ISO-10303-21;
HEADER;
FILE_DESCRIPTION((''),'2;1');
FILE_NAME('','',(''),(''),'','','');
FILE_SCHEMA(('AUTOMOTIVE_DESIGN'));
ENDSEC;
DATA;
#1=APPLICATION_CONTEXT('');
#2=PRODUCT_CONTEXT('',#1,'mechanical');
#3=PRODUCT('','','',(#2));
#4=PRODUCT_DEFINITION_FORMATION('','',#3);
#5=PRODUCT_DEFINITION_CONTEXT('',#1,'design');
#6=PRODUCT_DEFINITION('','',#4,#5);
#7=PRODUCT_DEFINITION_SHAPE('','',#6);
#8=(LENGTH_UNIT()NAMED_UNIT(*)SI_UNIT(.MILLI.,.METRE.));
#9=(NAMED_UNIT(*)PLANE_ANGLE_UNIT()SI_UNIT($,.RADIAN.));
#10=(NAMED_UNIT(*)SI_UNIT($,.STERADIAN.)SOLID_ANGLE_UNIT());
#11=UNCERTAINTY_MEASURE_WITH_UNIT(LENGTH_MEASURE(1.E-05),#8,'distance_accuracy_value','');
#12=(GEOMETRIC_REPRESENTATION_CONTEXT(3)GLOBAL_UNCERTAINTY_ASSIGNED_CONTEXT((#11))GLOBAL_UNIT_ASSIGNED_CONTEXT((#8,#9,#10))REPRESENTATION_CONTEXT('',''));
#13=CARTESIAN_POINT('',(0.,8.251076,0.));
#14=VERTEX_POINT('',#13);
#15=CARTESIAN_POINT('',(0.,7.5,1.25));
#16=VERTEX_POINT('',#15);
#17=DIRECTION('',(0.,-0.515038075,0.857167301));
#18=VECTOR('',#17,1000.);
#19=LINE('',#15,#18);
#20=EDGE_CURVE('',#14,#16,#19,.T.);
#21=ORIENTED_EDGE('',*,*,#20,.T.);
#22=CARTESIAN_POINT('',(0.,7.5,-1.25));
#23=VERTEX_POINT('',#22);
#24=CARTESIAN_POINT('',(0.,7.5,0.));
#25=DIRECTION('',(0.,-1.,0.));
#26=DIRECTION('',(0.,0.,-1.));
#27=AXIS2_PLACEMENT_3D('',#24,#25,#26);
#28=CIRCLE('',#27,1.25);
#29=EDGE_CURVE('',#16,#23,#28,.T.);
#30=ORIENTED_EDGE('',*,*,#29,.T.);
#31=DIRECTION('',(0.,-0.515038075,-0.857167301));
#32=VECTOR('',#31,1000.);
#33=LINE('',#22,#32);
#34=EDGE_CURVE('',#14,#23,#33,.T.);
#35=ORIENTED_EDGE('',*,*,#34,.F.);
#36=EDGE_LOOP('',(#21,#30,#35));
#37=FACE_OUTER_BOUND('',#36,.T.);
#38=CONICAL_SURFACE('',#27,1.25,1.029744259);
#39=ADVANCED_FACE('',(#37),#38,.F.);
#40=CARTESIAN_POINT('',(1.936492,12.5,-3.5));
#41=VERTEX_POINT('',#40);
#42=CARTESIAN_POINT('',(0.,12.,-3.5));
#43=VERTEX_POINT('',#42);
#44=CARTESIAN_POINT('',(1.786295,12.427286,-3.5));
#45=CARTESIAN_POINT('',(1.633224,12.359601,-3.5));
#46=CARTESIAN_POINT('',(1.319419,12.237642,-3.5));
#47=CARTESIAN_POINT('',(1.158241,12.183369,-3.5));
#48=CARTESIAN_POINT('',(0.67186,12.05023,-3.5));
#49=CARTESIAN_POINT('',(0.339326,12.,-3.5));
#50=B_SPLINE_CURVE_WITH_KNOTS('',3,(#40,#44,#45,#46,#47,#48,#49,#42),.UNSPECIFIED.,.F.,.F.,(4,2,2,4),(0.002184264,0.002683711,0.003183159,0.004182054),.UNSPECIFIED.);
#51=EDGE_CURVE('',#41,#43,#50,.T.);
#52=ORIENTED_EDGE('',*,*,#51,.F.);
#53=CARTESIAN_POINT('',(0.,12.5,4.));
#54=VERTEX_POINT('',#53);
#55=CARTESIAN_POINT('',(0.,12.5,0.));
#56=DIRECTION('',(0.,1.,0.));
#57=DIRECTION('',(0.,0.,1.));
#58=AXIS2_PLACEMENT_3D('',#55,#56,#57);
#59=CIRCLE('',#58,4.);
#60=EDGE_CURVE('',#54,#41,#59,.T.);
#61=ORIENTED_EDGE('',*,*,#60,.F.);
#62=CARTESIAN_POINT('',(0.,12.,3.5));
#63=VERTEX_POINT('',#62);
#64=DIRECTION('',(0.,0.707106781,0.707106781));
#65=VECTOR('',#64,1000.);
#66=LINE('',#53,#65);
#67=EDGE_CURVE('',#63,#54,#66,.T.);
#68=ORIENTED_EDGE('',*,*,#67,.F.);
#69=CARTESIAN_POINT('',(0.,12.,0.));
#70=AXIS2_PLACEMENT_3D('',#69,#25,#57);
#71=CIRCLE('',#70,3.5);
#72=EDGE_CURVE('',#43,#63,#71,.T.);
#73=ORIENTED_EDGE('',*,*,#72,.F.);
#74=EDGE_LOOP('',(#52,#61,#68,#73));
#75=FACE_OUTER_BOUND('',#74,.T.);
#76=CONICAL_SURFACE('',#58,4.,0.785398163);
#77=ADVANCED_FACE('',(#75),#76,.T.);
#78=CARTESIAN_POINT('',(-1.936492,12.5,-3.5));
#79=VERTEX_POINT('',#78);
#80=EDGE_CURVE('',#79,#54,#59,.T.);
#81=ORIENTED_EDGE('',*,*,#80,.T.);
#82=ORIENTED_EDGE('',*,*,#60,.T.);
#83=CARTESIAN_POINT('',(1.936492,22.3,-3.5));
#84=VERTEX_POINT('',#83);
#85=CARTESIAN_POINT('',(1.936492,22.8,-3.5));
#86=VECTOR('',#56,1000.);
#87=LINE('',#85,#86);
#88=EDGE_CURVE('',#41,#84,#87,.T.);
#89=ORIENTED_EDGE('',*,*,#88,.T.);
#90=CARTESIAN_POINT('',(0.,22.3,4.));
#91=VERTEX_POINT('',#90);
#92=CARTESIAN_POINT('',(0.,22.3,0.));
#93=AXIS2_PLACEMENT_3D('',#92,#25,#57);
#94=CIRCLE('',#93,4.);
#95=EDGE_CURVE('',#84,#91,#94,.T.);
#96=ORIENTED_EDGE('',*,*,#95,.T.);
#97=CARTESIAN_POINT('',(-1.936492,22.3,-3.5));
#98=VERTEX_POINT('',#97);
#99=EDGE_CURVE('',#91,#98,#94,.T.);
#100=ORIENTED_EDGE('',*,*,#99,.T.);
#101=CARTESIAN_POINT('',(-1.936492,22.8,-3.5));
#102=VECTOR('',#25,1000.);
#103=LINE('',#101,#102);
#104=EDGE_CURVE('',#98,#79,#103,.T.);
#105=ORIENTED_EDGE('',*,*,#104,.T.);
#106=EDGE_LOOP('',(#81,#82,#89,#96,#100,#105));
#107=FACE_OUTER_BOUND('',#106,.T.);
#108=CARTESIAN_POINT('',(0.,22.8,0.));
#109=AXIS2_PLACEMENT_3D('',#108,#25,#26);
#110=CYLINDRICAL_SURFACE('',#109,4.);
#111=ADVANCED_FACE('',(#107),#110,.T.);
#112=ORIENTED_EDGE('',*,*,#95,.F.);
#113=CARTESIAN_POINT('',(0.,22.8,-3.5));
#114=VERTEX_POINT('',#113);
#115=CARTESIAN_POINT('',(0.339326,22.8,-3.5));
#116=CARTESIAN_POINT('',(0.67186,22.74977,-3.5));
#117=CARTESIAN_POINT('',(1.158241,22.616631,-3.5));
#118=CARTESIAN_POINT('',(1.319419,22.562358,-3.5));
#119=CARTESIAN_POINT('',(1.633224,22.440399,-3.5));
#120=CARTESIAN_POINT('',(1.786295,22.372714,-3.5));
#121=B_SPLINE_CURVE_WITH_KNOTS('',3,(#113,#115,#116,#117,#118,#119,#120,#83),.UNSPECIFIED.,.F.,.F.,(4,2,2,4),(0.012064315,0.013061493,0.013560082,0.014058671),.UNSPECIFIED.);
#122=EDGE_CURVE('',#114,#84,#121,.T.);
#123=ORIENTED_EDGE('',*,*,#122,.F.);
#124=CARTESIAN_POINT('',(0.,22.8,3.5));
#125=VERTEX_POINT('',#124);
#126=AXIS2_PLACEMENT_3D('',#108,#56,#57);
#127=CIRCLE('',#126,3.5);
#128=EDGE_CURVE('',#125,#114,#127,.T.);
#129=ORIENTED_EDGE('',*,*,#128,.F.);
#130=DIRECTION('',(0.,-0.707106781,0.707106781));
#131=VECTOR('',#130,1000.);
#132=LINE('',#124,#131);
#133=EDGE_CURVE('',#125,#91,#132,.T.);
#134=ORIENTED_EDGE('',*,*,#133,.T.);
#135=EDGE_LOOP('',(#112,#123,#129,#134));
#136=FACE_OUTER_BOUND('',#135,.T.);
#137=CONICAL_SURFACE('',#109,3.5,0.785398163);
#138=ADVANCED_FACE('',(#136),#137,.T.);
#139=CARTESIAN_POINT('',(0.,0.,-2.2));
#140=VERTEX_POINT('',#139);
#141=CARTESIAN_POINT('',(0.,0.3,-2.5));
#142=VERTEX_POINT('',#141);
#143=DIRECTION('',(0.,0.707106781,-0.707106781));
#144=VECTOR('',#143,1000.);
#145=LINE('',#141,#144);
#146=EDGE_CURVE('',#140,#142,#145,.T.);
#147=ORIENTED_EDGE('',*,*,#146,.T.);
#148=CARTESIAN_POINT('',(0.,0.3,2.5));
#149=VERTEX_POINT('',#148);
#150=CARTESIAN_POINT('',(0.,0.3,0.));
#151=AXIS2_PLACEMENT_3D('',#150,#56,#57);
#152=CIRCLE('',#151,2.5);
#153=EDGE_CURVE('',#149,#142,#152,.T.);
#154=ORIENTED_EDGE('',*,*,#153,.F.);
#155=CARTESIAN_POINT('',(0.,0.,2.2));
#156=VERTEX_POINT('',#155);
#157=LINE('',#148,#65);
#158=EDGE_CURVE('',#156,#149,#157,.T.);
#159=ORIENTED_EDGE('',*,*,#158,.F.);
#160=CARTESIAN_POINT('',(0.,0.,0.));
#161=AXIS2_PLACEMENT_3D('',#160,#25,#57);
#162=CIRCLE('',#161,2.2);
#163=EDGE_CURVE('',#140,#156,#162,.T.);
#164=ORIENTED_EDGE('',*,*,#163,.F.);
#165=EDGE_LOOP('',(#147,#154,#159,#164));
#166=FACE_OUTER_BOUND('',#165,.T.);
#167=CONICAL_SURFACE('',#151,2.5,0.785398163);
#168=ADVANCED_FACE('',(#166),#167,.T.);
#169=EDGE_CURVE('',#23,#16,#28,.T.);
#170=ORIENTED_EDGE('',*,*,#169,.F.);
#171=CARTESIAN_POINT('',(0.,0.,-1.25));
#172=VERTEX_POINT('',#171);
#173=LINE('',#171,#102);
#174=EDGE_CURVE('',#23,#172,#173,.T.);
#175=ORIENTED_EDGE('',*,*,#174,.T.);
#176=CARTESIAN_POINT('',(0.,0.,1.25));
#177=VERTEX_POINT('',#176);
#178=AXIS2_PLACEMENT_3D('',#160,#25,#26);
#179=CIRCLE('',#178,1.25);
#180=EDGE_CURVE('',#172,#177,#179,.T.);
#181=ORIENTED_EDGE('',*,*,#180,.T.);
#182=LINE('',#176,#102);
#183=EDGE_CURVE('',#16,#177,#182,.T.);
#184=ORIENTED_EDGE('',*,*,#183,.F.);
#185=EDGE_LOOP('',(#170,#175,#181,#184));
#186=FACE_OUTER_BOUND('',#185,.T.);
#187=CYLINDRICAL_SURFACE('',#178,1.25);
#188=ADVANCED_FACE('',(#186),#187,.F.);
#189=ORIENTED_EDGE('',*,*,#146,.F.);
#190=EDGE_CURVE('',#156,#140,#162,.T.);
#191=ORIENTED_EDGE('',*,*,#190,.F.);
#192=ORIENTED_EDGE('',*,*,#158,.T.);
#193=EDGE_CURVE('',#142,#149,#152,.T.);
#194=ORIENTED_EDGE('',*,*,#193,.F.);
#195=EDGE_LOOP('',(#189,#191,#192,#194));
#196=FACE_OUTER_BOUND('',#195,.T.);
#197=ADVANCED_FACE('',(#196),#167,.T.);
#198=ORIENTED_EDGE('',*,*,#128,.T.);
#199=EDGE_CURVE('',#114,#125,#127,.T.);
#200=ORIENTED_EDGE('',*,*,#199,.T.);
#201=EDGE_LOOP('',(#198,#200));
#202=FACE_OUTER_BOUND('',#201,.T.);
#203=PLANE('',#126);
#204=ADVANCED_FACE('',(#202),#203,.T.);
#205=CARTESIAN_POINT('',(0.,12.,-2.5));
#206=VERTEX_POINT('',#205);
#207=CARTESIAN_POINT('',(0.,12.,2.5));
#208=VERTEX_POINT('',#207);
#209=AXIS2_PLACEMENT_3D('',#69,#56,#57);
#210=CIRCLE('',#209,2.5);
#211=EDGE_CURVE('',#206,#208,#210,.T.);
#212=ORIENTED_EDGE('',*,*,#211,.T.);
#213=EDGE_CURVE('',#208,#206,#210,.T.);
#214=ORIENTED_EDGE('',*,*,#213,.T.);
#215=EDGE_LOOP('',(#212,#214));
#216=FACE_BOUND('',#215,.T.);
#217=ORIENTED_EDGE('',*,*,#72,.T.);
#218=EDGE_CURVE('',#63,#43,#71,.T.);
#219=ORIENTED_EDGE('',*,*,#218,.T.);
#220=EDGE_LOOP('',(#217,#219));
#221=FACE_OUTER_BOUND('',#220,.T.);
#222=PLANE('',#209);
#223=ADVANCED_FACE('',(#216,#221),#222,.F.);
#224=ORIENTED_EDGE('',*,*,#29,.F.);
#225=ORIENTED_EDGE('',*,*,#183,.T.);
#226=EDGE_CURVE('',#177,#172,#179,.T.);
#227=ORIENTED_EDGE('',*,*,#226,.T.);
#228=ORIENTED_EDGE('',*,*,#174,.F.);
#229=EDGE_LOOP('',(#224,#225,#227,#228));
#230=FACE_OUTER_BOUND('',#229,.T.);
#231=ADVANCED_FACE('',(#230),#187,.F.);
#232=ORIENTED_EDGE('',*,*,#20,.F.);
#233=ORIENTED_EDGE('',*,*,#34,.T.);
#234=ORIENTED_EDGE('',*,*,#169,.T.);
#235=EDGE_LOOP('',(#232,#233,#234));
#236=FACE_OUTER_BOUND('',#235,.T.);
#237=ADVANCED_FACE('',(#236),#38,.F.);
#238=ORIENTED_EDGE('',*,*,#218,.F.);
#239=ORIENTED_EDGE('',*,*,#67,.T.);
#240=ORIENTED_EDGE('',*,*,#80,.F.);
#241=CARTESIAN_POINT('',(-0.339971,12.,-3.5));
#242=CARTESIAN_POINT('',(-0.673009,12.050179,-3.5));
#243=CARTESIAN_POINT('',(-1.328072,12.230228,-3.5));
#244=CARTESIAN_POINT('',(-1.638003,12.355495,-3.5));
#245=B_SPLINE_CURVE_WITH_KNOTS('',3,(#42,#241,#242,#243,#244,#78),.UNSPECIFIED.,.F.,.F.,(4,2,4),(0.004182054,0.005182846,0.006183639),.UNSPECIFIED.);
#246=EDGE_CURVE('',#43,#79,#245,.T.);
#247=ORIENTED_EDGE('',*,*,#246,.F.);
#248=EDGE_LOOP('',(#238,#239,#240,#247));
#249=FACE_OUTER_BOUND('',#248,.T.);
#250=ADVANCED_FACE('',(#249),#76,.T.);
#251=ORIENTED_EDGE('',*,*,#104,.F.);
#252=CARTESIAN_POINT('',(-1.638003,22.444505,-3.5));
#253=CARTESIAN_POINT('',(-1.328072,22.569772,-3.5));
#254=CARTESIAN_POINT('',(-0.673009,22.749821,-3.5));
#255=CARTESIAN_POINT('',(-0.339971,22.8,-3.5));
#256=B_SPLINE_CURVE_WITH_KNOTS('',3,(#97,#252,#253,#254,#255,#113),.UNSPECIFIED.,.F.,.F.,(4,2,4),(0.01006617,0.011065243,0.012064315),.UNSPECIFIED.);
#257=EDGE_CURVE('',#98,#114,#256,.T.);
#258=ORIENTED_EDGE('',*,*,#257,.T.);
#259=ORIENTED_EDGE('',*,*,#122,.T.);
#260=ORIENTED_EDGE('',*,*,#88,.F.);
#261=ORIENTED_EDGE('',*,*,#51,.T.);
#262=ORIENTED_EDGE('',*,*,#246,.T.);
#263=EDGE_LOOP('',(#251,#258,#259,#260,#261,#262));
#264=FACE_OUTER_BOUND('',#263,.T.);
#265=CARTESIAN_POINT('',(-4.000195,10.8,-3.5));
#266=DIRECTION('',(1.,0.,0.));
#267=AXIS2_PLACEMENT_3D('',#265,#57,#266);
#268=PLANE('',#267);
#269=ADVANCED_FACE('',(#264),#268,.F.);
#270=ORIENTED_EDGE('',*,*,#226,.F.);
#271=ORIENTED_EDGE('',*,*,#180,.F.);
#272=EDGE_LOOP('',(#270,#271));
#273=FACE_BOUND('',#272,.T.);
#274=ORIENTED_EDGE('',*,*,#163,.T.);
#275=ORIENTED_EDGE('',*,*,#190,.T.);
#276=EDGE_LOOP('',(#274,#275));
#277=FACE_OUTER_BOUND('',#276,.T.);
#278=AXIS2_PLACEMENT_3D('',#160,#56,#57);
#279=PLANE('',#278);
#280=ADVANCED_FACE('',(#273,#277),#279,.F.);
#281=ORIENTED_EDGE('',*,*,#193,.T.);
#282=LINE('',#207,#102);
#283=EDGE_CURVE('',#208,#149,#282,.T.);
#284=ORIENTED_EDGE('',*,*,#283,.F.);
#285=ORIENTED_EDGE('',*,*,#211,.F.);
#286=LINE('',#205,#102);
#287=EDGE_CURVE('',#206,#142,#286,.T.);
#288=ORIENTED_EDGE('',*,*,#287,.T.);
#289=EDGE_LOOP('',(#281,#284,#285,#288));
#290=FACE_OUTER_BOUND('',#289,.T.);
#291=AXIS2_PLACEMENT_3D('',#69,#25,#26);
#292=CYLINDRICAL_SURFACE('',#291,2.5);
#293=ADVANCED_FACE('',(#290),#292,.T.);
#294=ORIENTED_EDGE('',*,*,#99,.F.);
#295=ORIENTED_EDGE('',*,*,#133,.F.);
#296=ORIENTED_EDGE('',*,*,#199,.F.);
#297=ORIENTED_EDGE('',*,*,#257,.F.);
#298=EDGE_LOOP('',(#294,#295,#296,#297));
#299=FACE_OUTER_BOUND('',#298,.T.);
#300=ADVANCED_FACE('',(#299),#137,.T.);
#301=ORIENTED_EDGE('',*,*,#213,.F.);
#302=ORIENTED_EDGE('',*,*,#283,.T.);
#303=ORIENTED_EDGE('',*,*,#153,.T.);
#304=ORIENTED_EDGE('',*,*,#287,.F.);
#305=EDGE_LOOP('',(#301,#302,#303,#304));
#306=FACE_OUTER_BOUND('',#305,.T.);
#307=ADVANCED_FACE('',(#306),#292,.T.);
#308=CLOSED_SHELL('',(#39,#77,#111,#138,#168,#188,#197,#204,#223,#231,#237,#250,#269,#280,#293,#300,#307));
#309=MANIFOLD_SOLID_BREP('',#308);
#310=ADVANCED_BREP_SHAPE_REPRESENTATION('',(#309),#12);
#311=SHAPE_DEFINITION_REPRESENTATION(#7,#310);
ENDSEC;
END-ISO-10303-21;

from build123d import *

# Parameters (mm, degrees)
SKETCH1_R             = 2.5
BOSS_EXTRUDE1_DEPTH   = 12
SKETCH2_R             = 4
BOSS_EXTRUDE2_DEPTH   = 10.8
CHAMFER1_SIZE         = 0.5
CHAMFER2_SIZE         = 0.3
SKETCH3_W             = 8.000389638
SKETCH3_H             = 1
CUT_EXTRUDE1_DEPTH    = 12
M3_TAPPED_HOLE1_D     = 2.5
M3_TAPPED_HOLE1_DEPTH = 7.5
M3_TAPPED_HOLE1_TIP   = 0.751075774


with BuildPart() as part:
    # Sketch1 → Boss-Extrude1 (new body)
    with BuildSketch(Plane(origin=(0, 0, 0), x_dir=(1, 0, 0), z_dir=(0, 1, 0))):
        with Locations(Location((0, 0, 0), (0, 0, 270))):
            Circle(SKETCH1_R)
    extrude(amount=BOSS_EXTRUDE1_DEPTH)

    # Sketch2 → Boss-Extrude2 (add)
    with BuildSketch(Plane(origin=(0, 12, 0), x_dir=(1, 0, 0), z_dir=(0, 1, 0))):
        with Locations(Location((0, 0, 0), (0, 0, 90))):
            Circle(SKETCH2_R)
    extrude(amount=BOSS_EXTRUDE2_DEPTH)

    # Chamfer1
    chamfer1_edges = [part.edges().sort_by_distance(p)[0] for p in [
        (0, 12, 4),
        (0, 22.8, 4),
    ]]
    chamfer(chamfer1_edges, length=CHAMFER1_SIZE)

    # Chamfer2
    chamfer2_edges = [part.edges().sort_by_distance(p)[0] for p in [
        (0, 0, -2.5),
    ]]
    chamfer(chamfer2_edges, length=CHAMFER2_SIZE)

    # Sketch3 → Cut-Extrude1 (cut)
    with BuildSketch(Plane(origin=(0, 22.8, 0), x_dir=(1, 0, 0), z_dir=(0, 1, 0))):
        with Locations((0, 4)):
            Rectangle(SKETCH3_W, SKETCH3_H)
    extrude(amount=-CUT_EXTRUDE1_DEPTH, mode=Mode.SUBTRACT)

    # M3 Tapped Hole1
    with Locations(Plane(origin=(0, 0, 0), x_dir=(-1, 0, 0), z_dir=(0, -1, 0))):
        with Locations((0, 0)):
            Hole(M3_TAPPED_HOLE1_D / 2, depth=M3_TAPPED_HOLE1_DEPTH)
            with Locations((0, 0, -(M3_TAPPED_HOLE1_DEPTH + M3_TAPPED_HOLE1_TIP / 2))):  # 118° drill point
                Cone(0, M3_TAPPED_HOLE1_D / 2, M3_TAPPED_HOLE1_TIP, mode=Mode.SUBTRACT)


solid = part.part
